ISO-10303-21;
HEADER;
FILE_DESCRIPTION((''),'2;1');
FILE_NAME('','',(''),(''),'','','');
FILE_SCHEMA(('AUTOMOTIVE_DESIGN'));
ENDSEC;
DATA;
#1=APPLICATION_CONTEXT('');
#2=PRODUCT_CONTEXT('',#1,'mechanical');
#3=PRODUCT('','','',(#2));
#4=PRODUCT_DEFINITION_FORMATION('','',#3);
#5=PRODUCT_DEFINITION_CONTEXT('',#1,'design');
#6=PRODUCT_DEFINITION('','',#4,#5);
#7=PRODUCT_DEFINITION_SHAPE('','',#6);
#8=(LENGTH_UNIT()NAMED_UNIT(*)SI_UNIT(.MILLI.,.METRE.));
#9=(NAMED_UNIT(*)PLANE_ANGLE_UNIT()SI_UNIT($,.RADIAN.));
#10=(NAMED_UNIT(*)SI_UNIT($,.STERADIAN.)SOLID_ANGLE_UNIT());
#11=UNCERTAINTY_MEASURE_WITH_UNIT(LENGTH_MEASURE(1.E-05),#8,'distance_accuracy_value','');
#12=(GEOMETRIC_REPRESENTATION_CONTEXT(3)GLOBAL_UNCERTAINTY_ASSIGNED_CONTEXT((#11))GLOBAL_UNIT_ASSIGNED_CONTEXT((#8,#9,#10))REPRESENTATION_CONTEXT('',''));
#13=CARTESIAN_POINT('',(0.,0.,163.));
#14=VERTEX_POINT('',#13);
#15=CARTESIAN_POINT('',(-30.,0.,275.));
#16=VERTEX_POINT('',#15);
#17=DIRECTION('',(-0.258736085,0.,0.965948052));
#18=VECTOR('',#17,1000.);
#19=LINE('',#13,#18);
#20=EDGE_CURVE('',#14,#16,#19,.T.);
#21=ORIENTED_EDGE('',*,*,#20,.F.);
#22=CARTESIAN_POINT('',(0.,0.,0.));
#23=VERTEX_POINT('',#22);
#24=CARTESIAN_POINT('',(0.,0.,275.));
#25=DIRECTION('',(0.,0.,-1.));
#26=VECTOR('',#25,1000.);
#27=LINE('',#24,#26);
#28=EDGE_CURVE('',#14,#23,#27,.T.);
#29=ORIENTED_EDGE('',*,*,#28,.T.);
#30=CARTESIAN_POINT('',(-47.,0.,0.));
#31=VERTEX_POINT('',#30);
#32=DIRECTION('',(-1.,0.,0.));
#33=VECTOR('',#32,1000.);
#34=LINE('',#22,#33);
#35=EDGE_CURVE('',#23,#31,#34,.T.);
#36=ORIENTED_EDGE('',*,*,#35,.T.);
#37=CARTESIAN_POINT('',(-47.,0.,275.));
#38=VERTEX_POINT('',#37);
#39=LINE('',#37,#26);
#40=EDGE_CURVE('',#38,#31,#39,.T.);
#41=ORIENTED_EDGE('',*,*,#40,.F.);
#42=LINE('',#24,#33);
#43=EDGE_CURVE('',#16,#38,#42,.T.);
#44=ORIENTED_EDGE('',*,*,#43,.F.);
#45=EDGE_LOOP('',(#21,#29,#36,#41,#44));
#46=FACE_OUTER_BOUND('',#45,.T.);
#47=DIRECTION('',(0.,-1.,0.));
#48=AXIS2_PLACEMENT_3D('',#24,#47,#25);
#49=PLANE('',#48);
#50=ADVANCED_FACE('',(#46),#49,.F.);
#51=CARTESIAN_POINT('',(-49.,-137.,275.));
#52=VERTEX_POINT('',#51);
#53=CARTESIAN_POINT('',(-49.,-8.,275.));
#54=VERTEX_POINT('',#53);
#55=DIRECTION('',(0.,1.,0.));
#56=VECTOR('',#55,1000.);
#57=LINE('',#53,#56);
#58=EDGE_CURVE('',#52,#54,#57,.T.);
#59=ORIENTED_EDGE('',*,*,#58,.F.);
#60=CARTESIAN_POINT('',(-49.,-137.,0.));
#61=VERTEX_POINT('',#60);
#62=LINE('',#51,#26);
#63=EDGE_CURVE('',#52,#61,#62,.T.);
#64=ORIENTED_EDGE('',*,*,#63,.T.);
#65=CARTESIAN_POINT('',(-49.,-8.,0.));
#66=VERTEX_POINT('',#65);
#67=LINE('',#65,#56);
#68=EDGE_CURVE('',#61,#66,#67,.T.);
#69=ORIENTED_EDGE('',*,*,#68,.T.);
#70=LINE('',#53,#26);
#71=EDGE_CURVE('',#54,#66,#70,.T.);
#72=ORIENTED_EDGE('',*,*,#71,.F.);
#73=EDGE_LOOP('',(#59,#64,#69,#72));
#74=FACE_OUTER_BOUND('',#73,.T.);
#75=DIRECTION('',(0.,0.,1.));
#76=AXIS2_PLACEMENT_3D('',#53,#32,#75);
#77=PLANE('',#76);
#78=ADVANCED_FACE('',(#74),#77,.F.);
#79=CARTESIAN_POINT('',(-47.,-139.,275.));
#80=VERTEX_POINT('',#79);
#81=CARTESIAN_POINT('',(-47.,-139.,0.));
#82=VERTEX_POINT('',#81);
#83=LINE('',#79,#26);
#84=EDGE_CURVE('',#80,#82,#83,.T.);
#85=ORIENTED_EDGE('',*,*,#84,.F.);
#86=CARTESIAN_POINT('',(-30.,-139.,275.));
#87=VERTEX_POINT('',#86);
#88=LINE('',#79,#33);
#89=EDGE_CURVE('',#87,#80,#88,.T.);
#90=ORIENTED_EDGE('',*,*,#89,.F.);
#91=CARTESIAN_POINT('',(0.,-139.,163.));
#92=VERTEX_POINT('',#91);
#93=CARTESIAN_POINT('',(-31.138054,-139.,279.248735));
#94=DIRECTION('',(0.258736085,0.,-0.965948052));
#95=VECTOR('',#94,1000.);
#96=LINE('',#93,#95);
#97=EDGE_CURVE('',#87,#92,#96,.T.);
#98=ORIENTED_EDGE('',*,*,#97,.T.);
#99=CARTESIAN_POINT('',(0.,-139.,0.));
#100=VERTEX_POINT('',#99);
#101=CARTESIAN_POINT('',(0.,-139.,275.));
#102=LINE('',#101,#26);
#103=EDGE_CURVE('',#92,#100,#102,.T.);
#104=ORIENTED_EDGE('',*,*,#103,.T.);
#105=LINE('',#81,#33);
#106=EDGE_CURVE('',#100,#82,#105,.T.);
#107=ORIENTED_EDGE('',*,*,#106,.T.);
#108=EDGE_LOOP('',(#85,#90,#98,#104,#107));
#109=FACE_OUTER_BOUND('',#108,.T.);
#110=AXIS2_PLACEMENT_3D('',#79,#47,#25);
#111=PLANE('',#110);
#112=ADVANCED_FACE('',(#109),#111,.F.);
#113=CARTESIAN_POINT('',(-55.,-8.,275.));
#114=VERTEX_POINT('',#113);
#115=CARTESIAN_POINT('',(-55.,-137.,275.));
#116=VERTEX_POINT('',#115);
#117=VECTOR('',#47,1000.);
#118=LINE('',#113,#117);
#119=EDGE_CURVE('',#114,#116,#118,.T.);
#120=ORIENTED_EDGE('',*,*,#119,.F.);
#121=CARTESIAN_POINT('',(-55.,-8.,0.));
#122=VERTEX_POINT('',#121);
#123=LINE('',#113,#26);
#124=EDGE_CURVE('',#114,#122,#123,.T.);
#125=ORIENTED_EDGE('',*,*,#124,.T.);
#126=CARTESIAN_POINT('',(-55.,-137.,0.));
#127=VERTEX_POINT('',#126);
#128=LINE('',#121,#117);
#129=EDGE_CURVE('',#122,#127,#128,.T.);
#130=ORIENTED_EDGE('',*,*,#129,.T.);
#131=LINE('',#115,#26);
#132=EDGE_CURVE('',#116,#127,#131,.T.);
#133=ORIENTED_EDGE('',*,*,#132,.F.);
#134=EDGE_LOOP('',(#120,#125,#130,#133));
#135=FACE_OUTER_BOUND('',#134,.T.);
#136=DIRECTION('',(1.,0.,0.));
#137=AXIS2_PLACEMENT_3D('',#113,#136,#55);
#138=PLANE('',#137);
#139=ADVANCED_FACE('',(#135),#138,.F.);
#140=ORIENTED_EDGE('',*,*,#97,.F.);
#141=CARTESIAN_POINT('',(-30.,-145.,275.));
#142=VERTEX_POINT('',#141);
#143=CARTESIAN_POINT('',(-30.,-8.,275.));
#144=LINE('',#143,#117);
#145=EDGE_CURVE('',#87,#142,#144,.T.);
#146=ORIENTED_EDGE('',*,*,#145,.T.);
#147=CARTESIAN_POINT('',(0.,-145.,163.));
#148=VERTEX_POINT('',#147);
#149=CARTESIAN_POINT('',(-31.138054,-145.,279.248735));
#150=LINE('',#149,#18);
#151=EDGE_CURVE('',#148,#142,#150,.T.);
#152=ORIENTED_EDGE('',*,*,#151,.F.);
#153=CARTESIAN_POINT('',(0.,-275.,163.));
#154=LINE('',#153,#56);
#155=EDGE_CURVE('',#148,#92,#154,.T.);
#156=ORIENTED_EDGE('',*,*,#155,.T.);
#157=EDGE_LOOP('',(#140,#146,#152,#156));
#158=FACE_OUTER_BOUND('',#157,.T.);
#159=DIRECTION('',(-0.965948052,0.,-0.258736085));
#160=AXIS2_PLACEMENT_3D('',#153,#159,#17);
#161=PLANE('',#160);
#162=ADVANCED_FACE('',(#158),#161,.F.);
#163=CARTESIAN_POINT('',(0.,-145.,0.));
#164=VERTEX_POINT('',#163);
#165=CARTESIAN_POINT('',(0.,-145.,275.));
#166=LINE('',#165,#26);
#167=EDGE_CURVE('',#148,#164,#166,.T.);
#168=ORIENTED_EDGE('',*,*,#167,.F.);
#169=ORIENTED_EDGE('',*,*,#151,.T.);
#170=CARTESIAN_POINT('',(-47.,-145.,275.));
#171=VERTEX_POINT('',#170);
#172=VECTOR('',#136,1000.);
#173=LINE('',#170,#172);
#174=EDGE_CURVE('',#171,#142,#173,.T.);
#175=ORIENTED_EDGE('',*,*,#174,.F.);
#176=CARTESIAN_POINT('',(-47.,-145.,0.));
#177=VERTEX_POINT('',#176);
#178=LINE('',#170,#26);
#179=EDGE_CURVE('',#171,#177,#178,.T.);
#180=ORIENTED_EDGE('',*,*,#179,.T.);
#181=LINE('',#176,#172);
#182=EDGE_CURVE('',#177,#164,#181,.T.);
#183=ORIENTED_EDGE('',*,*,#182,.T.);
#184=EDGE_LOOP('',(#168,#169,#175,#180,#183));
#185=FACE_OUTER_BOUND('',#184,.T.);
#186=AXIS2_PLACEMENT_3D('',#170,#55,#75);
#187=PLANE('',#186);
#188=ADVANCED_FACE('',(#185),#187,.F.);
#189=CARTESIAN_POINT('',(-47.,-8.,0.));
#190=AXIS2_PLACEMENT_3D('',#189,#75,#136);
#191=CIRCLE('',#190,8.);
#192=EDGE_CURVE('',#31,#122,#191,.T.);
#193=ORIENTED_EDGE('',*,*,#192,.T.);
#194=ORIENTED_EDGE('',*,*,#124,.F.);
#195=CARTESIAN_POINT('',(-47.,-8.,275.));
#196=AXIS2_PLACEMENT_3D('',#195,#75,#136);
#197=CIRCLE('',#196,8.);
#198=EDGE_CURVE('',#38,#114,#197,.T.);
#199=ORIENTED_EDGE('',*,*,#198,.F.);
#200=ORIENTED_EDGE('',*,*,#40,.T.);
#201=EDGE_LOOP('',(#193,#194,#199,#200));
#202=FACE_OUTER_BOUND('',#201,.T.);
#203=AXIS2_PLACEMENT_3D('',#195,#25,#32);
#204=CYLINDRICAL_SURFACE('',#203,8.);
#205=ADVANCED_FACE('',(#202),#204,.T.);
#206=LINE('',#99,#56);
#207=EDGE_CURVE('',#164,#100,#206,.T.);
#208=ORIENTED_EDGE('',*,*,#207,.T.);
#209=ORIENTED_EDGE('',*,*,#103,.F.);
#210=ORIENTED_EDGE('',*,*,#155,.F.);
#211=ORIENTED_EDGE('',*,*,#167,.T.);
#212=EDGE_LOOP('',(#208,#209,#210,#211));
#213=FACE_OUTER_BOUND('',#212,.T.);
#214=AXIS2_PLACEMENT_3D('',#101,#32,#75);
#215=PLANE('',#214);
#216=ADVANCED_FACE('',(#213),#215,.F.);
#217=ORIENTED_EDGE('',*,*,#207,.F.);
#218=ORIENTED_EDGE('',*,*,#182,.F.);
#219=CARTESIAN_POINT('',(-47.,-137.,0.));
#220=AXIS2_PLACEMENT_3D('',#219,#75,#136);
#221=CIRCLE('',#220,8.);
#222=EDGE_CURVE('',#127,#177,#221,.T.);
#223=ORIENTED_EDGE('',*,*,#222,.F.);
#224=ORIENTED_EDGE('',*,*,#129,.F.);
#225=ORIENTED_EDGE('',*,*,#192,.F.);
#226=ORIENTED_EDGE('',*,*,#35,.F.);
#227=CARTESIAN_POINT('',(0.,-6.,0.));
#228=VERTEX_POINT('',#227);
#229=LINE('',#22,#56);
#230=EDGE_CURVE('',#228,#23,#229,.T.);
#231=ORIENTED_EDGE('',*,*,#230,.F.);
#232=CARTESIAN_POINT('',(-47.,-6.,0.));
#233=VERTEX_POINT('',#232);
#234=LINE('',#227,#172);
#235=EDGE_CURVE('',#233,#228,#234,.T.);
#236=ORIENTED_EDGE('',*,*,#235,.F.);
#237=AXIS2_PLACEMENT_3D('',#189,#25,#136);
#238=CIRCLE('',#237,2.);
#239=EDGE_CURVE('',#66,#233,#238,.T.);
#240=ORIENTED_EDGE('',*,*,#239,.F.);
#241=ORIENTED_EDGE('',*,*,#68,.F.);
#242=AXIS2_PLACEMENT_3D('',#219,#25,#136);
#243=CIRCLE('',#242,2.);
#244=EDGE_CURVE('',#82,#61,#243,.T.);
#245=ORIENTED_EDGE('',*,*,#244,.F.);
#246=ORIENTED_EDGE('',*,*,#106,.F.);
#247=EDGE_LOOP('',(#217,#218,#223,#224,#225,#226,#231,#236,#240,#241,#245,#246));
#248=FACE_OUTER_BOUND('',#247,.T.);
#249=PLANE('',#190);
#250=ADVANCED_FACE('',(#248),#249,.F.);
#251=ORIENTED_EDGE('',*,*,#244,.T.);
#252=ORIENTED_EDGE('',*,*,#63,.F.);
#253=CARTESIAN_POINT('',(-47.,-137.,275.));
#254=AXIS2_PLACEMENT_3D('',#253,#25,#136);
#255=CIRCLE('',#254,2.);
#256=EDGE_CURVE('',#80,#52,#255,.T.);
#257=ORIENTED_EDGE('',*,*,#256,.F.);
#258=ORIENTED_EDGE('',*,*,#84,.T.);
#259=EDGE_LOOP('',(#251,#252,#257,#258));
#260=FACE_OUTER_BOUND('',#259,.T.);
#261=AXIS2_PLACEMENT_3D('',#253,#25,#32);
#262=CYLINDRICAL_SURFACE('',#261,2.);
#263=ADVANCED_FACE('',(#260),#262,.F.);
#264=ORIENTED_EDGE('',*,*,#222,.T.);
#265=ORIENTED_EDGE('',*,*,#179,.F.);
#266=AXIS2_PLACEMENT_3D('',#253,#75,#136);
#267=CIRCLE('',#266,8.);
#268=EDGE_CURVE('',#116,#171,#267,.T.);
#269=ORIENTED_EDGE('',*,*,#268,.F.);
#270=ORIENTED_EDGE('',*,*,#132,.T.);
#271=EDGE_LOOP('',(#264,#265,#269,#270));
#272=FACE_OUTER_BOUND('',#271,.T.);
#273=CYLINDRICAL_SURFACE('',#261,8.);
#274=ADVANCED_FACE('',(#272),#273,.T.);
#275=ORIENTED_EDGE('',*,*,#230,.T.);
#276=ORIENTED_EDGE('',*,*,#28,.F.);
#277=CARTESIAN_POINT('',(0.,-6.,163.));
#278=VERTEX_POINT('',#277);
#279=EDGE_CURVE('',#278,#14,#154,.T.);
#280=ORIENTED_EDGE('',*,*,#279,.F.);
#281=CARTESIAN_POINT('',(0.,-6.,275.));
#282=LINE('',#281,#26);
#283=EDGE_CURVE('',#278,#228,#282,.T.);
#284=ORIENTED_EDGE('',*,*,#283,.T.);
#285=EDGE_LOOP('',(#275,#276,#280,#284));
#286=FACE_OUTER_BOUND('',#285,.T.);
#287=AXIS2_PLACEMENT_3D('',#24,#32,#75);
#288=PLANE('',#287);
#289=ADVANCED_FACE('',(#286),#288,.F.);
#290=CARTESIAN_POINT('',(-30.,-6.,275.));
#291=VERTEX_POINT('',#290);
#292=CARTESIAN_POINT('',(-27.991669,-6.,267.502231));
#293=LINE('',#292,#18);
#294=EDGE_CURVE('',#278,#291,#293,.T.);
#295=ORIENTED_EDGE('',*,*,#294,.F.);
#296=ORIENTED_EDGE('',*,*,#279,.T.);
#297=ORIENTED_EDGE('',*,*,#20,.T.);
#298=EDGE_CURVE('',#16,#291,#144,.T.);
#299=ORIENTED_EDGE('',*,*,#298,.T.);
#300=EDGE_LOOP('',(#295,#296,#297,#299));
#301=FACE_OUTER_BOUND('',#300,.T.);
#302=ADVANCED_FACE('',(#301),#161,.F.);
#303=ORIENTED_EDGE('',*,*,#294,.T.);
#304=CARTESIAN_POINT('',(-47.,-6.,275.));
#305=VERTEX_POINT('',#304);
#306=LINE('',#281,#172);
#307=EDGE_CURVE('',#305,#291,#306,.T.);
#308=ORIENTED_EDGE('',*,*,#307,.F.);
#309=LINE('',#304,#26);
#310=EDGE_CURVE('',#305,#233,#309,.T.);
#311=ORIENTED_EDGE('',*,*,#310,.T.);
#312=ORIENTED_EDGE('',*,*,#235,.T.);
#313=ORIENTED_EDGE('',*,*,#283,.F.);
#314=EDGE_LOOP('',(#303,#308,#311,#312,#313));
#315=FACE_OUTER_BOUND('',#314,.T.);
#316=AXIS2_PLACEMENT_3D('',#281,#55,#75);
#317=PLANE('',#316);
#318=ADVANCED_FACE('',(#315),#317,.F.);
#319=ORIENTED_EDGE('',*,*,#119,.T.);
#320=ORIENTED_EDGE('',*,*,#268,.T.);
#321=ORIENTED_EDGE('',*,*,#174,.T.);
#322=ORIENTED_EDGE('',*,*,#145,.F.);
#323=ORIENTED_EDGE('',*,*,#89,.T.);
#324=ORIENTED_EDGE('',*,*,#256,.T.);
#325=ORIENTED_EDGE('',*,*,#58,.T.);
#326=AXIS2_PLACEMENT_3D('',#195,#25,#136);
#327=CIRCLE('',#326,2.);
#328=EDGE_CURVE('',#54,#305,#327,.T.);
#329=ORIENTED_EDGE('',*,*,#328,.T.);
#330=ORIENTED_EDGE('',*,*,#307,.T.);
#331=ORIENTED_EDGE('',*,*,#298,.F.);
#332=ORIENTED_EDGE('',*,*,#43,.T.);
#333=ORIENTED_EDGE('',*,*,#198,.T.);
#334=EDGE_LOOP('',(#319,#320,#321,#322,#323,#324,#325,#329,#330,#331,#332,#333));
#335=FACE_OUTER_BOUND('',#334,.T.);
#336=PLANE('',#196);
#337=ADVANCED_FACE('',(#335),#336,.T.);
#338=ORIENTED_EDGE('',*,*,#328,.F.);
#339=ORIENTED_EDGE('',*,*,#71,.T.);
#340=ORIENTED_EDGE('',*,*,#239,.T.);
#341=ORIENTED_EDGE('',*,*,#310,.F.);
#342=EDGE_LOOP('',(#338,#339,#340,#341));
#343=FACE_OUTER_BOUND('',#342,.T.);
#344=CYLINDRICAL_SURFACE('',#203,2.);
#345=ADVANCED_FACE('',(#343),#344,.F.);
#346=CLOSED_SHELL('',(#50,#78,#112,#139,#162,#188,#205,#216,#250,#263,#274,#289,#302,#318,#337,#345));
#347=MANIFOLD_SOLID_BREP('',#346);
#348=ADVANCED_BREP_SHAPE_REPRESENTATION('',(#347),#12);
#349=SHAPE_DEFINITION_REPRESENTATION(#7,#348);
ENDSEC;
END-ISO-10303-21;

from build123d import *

# Parameters (mm, degrees)
EXTRUDE_1_DEPTH     = 275
CUT_EXTRUDE_1_DEPTH = 275


with BuildPart() as part:
    # 草图1 → 凸台-拉伸1 (new body)
    with BuildSketch(Plane.XY):
        with BuildLine():
            Line((0, 0), (-47, 0))
            ThreePointArc((-47, 0), (-52.656854249, -2.343145751), (-55, -8))
            Line((-55, -8), (-55, -137))
            ThreePointArc((-55, -137), (-52.656854249, -142.656854249), (-47, -145))
            Line((-47, -145), (0, -145))
            Line((0, -145), (0, -139))
            Line((0, -139), (-47, -139))
            ThreePointArc((-47, -139), (-48.414213562, -138.414213562), (-49, -137))
            Line((-49, -137), (-49, -8))
            ThreePointArc((-49, -8), (-48.414213562, -6.585786438), (-47, -6))
            Line((-47, -6), (0, -6))
            Line((0, -6), (0, 0))
        make_face()
    extrude(amount=EXTRUDE_1_DEPTH)

    # 草图2 → 切除-拉伸1 (cut)
    with BuildSketch(Plane(origin=(0, 0, 0), x_dir=(1, 0, 0), z_dir=(0, 1, 0))):
        Polygon((0, -163), (-30, -275), (0, -275), align=None)
    extrude(amount=-CUT_EXTRUDE_1_DEPTH, mode=Mode.SUBTRACT)


solid = part.part
